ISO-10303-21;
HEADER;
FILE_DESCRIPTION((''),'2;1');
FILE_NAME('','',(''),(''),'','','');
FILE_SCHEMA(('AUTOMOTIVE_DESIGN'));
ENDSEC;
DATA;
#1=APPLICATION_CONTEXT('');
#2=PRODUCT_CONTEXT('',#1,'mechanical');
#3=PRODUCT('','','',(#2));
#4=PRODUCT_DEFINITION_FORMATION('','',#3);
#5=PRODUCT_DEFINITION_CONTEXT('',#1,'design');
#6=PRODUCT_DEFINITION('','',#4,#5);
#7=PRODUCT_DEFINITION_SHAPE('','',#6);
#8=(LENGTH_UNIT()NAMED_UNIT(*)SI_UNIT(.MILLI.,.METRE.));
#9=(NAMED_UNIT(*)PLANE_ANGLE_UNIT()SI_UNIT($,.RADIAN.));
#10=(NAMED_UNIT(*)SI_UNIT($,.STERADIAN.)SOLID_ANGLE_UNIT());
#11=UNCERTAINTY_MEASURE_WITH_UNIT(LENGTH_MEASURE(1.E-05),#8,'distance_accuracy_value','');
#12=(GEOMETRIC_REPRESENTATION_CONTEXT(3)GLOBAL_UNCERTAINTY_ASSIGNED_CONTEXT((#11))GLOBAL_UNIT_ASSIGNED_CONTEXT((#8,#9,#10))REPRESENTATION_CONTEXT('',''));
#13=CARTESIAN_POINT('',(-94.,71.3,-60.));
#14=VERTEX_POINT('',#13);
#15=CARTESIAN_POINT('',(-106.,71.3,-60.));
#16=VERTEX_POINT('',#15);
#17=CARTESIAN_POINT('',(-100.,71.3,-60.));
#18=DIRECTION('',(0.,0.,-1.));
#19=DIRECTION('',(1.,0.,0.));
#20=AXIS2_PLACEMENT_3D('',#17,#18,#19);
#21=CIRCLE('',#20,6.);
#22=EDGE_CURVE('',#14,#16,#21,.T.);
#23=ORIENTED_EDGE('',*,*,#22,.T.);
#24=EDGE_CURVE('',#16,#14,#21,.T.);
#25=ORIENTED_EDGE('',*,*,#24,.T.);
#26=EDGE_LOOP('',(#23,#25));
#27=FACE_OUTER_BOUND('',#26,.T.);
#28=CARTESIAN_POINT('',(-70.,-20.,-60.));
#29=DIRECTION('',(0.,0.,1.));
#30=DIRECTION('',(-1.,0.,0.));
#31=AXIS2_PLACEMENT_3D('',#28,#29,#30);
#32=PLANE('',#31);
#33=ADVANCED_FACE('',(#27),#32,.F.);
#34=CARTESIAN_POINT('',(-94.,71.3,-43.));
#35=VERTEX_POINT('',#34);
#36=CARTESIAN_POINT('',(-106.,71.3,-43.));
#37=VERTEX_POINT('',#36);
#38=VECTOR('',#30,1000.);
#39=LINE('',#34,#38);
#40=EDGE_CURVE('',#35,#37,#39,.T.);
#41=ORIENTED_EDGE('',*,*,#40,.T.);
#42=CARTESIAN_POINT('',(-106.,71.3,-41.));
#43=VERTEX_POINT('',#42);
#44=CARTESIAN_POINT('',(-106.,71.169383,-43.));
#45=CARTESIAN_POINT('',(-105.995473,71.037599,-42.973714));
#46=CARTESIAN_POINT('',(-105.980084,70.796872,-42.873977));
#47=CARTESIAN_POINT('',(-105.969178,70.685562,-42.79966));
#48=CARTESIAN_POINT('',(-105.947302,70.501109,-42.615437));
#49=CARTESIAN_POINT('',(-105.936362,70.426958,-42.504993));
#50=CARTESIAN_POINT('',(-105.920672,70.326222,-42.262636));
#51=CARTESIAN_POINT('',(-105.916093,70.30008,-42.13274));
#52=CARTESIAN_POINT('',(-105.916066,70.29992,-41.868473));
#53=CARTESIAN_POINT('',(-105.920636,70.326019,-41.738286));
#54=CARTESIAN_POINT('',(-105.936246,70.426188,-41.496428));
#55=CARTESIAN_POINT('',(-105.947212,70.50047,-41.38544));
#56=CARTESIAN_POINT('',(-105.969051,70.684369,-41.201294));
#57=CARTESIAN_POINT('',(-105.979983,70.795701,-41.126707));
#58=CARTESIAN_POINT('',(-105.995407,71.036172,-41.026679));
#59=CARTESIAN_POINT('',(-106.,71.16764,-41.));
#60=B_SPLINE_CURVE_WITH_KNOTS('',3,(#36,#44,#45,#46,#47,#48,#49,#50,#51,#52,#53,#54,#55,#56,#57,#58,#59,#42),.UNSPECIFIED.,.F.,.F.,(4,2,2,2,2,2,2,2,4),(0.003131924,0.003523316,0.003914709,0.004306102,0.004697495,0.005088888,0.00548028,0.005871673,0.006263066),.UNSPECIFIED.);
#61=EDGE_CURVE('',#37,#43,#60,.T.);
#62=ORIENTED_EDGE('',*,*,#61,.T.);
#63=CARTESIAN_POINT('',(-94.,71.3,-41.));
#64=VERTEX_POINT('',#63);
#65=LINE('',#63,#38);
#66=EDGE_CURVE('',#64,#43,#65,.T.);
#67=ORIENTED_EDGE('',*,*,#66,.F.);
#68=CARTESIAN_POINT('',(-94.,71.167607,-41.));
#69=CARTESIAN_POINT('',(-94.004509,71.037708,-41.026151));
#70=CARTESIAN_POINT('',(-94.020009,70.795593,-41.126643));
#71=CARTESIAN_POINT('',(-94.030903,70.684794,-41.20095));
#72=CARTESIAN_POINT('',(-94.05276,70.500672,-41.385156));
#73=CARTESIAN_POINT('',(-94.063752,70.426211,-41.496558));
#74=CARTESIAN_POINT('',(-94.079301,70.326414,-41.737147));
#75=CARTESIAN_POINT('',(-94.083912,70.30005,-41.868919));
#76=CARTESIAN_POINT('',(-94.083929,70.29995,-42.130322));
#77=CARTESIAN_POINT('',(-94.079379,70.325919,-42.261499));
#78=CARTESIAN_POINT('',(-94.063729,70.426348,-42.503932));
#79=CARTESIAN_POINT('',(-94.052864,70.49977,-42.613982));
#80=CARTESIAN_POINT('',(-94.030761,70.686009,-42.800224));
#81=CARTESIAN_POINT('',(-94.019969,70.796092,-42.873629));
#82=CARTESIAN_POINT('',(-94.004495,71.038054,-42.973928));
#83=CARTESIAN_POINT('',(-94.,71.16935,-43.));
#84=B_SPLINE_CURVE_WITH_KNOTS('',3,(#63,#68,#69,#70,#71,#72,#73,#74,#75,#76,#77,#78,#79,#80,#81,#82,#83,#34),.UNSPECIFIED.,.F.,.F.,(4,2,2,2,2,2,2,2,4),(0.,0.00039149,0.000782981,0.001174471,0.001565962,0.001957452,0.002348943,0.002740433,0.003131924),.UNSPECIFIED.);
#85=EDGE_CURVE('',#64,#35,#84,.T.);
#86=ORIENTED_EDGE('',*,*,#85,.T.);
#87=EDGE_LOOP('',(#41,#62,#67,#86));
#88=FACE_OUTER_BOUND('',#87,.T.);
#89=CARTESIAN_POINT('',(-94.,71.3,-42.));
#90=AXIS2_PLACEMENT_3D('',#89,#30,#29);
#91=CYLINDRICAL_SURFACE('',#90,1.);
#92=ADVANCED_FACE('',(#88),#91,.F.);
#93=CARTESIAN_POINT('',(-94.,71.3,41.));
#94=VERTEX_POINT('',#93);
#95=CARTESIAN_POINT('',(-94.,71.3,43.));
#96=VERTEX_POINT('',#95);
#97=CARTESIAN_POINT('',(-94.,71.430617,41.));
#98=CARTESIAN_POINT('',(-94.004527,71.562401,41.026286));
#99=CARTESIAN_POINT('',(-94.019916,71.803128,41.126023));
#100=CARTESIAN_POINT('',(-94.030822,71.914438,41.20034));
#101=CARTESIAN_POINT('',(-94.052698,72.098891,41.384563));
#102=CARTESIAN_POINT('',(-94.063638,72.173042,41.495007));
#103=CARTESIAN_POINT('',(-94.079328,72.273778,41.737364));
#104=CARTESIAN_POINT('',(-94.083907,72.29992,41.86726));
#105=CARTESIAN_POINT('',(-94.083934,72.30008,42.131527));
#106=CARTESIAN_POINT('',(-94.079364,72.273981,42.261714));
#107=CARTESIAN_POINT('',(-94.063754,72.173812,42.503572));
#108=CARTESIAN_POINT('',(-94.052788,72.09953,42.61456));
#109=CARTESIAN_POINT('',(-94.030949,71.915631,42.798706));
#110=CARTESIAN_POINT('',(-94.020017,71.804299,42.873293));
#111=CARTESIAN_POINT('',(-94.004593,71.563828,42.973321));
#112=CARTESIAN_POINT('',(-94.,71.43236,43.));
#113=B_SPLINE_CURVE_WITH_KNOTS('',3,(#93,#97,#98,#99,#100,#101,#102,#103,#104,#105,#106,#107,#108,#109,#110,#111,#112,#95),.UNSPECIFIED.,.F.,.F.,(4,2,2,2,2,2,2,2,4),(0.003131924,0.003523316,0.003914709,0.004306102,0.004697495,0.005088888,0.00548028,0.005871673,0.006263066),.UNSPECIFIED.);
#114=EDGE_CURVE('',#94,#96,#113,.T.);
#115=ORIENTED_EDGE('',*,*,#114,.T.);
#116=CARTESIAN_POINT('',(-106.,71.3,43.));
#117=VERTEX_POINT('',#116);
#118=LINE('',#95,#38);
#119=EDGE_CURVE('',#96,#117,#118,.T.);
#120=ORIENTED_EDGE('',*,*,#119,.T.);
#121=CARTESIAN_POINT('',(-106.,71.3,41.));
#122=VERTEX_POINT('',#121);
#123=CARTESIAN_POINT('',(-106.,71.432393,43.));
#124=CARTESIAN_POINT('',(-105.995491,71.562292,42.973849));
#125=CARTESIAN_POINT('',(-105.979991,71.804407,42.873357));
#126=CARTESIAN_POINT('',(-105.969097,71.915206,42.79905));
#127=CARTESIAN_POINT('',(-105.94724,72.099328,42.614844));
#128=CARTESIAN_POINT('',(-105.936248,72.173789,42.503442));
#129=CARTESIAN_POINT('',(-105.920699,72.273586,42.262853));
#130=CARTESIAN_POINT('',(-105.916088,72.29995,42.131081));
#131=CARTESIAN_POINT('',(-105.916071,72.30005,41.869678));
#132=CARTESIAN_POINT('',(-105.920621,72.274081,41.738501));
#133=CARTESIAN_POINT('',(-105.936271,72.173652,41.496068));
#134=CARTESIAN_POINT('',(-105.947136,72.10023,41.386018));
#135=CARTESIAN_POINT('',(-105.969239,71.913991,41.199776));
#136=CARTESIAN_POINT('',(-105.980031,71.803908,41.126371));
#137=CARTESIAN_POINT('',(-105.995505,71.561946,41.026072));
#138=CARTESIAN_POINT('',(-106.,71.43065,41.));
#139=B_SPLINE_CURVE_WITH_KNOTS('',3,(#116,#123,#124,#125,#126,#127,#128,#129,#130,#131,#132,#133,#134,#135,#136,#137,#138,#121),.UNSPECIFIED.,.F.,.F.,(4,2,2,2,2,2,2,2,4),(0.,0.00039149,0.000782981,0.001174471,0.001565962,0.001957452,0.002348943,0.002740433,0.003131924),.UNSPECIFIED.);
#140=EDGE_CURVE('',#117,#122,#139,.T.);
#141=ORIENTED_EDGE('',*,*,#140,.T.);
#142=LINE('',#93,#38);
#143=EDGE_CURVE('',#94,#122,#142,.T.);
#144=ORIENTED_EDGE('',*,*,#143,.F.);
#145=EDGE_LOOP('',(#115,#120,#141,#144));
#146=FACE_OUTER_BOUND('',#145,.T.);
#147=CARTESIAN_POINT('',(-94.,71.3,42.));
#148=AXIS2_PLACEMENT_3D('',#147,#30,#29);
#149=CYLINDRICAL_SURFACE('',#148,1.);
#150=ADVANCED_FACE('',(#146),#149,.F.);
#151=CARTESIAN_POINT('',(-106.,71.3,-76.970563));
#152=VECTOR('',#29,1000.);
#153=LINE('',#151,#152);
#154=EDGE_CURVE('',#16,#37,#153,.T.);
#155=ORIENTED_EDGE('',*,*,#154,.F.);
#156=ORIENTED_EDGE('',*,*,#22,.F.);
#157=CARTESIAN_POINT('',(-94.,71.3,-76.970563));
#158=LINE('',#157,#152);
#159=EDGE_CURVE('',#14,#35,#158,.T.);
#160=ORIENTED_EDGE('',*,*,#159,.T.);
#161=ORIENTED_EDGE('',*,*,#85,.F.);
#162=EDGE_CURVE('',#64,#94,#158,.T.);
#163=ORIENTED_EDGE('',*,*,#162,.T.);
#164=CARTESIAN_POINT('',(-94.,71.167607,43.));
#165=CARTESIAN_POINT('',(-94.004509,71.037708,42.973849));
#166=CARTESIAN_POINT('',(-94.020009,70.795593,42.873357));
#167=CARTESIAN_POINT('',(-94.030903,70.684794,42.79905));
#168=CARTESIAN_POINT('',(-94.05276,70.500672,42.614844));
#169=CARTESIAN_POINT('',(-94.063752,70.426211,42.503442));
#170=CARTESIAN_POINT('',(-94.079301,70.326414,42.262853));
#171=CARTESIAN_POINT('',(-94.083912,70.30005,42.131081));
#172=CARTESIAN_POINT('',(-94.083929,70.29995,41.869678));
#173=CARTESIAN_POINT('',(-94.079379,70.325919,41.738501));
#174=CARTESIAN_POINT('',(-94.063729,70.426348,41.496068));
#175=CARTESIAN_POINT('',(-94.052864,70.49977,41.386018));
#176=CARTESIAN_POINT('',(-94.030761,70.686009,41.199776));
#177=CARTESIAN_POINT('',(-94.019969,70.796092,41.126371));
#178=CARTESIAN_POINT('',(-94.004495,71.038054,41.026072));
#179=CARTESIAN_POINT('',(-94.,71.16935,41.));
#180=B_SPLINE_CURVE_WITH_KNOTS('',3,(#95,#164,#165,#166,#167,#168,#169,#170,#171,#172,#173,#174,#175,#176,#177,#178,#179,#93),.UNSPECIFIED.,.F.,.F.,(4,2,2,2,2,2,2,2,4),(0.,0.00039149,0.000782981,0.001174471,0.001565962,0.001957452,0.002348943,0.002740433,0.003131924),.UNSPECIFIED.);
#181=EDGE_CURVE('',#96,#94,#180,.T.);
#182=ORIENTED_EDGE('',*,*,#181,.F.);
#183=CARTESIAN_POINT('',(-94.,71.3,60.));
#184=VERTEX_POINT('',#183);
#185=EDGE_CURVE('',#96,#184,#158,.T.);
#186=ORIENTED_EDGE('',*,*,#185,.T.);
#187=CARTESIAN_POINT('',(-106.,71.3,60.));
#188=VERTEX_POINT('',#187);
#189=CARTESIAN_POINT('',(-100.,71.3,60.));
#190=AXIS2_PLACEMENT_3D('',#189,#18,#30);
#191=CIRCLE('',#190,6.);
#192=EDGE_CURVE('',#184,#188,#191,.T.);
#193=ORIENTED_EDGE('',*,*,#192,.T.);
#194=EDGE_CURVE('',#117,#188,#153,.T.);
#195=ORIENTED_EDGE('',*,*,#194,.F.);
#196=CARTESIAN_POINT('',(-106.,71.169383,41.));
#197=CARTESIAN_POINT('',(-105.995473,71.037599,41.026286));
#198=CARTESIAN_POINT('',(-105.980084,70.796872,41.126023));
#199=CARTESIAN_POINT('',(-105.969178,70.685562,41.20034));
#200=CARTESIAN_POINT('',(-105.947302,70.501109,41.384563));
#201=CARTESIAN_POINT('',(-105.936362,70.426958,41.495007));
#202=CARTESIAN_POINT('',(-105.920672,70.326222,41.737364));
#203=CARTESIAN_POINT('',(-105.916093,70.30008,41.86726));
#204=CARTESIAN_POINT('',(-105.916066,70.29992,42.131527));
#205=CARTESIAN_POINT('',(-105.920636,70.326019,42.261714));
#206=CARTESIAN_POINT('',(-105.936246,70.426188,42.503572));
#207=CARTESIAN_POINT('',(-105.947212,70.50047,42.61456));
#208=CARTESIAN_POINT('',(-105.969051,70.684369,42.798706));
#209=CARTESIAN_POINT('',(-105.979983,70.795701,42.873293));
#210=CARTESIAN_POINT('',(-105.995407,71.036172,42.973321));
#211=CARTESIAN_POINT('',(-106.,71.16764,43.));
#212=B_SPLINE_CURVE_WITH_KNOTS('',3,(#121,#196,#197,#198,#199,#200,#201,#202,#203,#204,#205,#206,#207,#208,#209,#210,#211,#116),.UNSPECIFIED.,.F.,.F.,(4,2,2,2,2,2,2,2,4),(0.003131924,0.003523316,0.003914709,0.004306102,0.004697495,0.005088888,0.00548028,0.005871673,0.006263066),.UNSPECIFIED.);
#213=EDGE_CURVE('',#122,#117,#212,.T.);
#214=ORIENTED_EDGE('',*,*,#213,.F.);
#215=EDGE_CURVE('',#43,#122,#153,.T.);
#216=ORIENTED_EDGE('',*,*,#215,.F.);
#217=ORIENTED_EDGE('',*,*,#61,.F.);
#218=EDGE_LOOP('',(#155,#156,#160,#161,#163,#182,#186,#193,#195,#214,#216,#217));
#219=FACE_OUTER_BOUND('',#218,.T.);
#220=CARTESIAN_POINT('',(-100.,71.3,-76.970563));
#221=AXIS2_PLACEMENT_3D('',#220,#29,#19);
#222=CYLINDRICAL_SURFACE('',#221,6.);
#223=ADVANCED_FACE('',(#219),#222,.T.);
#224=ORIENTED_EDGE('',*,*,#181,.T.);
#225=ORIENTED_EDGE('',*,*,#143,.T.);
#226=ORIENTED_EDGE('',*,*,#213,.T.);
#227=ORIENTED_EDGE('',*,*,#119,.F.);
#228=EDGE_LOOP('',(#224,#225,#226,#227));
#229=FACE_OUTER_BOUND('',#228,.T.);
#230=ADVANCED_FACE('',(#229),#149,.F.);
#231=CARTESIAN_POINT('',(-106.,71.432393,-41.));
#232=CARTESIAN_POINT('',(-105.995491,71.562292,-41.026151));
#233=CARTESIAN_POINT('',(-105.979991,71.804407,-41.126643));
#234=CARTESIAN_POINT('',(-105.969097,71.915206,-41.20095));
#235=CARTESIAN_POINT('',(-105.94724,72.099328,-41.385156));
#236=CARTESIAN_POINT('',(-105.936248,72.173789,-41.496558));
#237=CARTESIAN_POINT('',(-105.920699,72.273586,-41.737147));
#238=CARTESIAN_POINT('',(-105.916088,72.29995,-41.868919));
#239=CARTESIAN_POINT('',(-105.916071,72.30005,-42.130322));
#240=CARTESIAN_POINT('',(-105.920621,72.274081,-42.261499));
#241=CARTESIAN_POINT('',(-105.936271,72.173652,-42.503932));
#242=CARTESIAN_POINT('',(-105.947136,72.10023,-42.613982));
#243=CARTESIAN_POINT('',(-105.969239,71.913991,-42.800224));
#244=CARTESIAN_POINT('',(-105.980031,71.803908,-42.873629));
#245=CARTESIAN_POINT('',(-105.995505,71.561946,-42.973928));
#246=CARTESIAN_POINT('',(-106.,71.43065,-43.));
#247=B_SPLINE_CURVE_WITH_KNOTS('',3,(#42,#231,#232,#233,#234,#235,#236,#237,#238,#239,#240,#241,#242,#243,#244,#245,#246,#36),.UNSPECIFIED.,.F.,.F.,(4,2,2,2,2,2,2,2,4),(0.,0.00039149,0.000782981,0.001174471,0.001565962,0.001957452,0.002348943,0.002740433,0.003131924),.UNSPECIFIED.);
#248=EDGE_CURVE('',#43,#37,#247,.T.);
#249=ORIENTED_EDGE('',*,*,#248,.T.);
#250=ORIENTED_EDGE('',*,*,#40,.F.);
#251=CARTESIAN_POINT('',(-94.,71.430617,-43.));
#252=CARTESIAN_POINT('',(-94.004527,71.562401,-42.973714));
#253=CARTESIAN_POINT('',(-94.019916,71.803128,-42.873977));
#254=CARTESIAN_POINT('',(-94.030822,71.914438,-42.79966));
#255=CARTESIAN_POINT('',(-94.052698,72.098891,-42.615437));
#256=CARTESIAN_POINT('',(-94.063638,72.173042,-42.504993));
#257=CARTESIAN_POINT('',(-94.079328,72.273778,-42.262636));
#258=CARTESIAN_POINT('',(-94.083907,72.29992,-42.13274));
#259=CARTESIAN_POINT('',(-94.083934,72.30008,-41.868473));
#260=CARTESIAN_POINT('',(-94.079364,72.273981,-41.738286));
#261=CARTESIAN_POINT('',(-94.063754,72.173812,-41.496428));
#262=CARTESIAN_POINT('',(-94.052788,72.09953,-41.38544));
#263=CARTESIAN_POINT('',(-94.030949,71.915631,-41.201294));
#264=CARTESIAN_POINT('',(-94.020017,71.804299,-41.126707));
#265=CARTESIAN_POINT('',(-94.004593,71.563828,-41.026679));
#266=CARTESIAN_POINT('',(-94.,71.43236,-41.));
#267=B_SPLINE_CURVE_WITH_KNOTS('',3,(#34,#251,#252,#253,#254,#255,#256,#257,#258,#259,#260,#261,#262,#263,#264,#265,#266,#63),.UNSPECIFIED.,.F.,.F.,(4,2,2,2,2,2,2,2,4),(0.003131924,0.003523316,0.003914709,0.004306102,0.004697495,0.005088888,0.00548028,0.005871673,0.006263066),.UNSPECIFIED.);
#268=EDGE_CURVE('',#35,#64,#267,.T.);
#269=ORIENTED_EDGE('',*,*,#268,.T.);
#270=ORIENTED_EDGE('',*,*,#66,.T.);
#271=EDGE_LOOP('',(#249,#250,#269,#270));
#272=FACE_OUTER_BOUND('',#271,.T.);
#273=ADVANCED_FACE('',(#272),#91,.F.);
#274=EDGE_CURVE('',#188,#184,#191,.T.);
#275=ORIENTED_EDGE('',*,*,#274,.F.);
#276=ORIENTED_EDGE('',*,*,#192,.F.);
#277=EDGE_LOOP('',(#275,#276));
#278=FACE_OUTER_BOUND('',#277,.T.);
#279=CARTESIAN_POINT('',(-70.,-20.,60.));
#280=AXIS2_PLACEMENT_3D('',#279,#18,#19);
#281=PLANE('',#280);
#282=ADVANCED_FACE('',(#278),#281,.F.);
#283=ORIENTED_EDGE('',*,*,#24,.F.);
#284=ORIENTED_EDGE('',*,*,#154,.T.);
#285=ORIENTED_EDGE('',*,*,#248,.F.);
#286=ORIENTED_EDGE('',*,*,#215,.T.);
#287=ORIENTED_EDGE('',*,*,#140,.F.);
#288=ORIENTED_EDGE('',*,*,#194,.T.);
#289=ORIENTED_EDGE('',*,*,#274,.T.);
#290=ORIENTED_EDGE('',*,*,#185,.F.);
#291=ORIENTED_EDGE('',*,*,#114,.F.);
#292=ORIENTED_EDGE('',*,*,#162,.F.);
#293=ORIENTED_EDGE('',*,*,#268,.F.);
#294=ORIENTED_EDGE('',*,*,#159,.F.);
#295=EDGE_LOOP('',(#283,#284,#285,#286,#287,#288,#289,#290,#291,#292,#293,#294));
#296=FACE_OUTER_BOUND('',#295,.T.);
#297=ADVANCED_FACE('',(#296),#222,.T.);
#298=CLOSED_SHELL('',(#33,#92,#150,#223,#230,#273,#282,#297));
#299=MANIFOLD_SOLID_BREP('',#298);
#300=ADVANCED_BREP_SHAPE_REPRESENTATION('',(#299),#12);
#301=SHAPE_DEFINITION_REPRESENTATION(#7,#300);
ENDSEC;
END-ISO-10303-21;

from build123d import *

# Parameters (mm, degrees)
BOSS_EXTRUDE1_DEPTH      = 60
BOSS_EXTRUDE1_DEPTH_BACK = 60
SKETCH1_R                = 6
CUT_EXTRUDE1_DEPTH       = 99.037186822
CUT_EXTRUDE1_DEPTH_BACK  = 99.037186822
SKETCH2_R                = 1


with BuildPart() as part:
    # Sketch1 → Boss-Extrude1 (new, two sides: drawn at the far end of the back side and taken through both)
    with BuildSketch(Plane.XY.offset(-BOSS_EXTRUDE1_DEPTH_BACK)):
        with Locations((-100, 71.3)):
            Circle(SKETCH1_R)
    extrude(amount=BOSS_EXTRUDE1_DEPTH + BOSS_EXTRUDE1_DEPTH_BACK)

    # Sketch2 → Cut-Extrude1 (cut, two sides: drawn at the far end of the back side and taken through both)
    with BuildSketch(Plane.ZY.offset(100).offset(-CUT_EXTRUDE1_DEPTH_BACK)):
        with Locations((-42, 71.3)):
            Circle(SKETCH2_R)
        with Locations((42, 71.3)):
            Circle(SKETCH2_R)
    extrude(amount=CUT_EXTRUDE1_DEPTH + CUT_EXTRUDE1_DEPTH_BACK, mode=Mode.SUBTRACT)


solid = part.part
